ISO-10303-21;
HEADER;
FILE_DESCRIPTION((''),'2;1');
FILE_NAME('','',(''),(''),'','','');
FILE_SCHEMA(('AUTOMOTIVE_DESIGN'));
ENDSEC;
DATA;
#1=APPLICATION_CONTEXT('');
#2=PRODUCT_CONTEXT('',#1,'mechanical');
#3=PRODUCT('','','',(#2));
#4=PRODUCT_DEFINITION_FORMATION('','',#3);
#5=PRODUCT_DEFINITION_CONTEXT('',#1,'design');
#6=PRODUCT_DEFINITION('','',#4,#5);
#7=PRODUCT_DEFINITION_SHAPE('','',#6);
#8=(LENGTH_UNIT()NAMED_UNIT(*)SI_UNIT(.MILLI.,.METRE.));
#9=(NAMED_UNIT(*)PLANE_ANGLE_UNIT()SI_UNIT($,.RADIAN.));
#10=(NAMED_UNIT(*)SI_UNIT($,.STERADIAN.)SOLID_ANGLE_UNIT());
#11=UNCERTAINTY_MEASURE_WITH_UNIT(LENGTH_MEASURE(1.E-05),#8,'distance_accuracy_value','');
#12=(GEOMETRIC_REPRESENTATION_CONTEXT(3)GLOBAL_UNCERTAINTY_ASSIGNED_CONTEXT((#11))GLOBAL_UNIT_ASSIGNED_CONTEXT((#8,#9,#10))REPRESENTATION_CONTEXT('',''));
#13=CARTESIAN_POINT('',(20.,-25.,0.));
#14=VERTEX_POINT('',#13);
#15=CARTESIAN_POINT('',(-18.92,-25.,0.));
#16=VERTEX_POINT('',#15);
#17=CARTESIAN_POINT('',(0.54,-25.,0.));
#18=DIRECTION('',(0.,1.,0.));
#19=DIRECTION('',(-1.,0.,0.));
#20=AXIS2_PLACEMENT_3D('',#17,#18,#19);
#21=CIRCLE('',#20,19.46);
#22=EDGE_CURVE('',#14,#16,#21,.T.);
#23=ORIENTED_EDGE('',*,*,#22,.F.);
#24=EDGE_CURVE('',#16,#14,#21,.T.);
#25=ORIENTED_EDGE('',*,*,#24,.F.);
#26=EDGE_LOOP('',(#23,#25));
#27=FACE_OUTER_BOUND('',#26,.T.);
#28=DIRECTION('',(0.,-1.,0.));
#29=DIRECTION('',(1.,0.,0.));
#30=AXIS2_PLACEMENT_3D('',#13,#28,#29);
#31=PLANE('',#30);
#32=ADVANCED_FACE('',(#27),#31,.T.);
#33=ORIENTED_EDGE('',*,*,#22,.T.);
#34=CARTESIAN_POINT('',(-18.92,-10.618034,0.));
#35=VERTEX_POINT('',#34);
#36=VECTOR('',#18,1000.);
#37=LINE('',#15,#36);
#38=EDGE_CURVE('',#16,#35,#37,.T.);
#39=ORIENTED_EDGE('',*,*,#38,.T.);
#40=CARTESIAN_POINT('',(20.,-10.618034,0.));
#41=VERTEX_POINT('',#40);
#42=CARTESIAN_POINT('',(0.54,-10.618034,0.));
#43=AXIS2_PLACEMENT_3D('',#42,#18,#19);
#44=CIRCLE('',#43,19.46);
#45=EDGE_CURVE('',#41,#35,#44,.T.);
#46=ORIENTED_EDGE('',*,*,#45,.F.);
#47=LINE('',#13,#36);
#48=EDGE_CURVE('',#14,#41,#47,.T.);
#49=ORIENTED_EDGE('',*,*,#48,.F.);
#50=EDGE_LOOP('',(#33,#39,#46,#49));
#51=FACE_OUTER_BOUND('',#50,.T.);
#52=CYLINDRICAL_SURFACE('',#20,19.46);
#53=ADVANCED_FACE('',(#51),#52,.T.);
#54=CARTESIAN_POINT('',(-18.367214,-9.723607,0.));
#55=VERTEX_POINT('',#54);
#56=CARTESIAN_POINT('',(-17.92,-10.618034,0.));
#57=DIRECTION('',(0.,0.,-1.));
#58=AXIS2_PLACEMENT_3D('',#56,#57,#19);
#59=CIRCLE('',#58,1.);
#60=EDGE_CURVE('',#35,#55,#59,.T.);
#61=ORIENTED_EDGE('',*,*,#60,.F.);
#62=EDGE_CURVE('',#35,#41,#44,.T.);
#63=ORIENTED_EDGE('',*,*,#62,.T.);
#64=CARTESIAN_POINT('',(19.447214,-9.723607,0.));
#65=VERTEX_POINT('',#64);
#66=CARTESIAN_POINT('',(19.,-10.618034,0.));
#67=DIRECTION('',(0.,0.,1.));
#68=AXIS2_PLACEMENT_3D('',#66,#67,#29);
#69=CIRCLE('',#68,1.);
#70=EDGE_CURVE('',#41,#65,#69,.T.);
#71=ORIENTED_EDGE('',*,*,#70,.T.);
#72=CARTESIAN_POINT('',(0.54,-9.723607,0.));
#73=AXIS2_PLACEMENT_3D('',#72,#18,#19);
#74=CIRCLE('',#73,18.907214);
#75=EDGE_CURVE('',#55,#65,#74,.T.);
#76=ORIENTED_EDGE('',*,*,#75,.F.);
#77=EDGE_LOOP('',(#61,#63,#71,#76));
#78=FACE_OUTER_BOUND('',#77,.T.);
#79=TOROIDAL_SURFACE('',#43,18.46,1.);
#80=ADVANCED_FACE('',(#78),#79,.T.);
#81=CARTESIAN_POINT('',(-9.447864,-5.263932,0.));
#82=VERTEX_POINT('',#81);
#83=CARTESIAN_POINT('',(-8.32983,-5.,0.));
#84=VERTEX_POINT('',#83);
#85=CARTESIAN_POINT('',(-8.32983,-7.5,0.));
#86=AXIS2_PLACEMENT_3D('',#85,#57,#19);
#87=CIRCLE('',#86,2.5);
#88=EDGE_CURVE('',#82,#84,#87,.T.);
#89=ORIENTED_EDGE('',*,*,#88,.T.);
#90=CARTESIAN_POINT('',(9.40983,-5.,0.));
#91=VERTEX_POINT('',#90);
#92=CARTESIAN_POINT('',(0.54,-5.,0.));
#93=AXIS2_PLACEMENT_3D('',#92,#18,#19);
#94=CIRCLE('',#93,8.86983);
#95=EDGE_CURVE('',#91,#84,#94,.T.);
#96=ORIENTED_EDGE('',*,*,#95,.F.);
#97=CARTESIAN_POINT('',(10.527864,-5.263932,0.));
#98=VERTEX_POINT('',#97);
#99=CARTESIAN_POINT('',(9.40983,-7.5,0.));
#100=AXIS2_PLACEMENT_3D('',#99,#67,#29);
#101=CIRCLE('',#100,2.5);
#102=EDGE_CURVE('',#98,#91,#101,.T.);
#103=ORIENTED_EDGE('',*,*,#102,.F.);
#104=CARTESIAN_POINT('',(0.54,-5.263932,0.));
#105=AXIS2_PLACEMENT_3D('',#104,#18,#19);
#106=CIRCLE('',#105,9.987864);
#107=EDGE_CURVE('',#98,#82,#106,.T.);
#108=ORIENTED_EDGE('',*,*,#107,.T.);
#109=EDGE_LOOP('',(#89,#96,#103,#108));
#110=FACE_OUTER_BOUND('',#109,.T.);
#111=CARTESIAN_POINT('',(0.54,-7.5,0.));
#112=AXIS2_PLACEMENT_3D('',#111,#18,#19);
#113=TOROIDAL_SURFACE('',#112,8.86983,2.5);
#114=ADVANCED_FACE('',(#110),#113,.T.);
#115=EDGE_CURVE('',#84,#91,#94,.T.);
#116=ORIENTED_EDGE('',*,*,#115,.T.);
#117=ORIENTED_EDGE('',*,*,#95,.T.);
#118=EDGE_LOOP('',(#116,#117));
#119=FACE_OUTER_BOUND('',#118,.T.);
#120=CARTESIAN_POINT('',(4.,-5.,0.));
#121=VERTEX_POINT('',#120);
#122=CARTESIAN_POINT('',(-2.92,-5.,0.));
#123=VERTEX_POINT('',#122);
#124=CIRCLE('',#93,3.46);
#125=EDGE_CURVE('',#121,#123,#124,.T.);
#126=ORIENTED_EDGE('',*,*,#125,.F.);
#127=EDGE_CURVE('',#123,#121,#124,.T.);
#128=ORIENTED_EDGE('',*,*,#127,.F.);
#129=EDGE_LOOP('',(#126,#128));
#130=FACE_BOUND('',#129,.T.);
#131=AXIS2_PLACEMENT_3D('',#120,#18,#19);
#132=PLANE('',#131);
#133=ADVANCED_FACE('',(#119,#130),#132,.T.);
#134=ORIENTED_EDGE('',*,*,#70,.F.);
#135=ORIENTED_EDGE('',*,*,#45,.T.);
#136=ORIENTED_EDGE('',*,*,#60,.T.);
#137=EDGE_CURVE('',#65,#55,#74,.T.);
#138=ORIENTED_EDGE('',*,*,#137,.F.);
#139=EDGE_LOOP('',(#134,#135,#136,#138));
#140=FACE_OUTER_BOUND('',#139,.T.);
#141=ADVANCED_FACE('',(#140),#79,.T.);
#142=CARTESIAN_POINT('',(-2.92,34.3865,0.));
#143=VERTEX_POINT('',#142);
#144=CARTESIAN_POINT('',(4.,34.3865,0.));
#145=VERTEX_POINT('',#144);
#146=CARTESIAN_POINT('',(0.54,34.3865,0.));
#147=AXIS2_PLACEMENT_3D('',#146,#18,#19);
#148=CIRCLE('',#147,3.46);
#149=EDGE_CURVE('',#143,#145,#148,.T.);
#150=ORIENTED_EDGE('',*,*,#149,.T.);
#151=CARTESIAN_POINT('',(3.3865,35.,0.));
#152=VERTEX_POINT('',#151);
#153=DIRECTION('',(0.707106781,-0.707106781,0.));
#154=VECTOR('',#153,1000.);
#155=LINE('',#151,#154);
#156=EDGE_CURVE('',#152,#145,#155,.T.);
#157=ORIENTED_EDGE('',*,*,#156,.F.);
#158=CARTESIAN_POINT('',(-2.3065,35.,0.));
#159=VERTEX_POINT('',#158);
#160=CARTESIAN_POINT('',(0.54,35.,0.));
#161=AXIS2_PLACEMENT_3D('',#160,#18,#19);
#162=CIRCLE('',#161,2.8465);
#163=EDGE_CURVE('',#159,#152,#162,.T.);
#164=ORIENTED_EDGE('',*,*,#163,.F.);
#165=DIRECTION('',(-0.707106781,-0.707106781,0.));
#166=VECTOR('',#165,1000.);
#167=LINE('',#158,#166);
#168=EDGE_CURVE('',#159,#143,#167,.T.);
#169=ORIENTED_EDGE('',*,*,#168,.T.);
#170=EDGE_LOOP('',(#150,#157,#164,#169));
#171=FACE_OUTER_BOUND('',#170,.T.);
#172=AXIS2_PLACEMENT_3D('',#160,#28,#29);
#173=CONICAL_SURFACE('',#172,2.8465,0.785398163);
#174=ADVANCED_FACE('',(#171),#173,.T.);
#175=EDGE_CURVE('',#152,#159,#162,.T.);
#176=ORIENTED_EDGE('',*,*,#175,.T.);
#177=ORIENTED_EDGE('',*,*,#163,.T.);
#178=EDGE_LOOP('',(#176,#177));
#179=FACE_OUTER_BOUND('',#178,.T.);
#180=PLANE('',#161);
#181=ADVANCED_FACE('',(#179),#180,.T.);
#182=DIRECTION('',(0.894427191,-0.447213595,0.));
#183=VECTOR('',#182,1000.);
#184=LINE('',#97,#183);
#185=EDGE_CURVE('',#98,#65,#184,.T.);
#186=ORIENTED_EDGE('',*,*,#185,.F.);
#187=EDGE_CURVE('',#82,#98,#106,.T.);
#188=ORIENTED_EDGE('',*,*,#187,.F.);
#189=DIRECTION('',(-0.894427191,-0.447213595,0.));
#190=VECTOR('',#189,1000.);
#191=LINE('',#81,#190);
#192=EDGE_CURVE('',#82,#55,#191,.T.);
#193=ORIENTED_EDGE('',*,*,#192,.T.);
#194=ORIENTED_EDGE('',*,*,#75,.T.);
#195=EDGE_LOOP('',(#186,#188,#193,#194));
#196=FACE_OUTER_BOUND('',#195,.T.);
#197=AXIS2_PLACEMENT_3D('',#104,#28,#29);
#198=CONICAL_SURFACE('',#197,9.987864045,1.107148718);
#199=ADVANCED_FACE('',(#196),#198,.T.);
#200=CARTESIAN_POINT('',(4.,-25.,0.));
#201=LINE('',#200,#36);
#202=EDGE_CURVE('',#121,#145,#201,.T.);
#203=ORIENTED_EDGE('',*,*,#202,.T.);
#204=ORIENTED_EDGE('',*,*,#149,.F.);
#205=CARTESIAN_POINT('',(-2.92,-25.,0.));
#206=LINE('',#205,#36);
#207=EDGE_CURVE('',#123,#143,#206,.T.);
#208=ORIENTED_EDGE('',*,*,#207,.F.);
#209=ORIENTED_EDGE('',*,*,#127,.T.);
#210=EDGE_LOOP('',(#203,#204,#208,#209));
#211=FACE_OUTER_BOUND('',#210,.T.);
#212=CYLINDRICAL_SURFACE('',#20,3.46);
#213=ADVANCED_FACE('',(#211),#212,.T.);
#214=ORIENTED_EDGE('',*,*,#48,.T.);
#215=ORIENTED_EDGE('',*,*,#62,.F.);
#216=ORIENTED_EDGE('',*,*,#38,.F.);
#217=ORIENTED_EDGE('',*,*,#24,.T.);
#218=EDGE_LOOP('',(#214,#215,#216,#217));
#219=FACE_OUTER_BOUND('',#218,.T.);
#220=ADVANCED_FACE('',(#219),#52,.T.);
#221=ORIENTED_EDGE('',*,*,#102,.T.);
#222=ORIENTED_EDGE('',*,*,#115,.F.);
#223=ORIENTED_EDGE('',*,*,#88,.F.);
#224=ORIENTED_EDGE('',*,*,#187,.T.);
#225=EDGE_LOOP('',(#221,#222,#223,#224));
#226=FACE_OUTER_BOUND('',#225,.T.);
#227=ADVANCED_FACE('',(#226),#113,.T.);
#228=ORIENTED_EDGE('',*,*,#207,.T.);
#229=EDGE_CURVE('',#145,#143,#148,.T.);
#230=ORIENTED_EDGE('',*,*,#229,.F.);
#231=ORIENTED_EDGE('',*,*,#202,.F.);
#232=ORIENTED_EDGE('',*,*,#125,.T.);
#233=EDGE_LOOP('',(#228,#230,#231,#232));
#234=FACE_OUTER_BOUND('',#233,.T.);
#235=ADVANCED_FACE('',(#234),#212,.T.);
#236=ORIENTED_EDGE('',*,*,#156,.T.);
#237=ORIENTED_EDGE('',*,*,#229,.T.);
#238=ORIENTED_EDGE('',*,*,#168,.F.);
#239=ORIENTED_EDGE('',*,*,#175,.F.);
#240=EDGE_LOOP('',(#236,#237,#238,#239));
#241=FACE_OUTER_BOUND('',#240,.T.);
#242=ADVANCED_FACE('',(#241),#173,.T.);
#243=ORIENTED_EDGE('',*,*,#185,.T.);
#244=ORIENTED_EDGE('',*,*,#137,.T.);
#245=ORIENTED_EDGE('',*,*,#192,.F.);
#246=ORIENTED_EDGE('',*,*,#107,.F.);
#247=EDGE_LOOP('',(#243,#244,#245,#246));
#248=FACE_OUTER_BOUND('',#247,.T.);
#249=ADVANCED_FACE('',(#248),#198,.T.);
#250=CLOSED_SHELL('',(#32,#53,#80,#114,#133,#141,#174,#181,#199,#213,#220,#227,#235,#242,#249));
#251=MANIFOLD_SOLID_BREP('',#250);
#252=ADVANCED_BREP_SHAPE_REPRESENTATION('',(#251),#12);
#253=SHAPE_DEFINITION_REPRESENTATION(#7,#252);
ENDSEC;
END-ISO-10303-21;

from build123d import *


with BuildPart() as part:
    # 草图1 → 旋转1 (revolve)
    with BuildSketch(Plane(origin=(0, 0, 0), x_dir=(-1, 0, 0), z_dir=(0, 0, -1)), mode=Mode.PRIVATE) as revolve_1_sk:
        with BuildLine():
            Line((-20, -25), (-0.54, -25))
            Line((-0.54, -25), (-0.54, 35))
            Line((-0.54, 35), (-3.3865, 35))
            Line((-3.3865, 35), (-4, 34.3865))
            Line((-4, 34.3865), (-4, -5))
            Line((-4, -5), (-9.409830056, -5))
            ThreePointArc((-9.409830056, -5), (-9.984212358, -5.066877526), (-10.527864045, -5.263932023))
            Line((-10.527864045, -5.263932023), (-19.447213595, -9.723606798))
            ThreePointArc((-19.447213595, -9.723606798), (-19.850650808, -10.092302877), (-20, -10.618033989))
            Line((-20, -10.618033989), (-20, -25))
        make_face()
    revolve(revolve_1_sk.sketch.rotate(Axis((0.54, -25, 0), (0, 1, 0)), 180), axis=Axis((0.54, -25, 0), (0, 1, 0)))


solid = part.part
